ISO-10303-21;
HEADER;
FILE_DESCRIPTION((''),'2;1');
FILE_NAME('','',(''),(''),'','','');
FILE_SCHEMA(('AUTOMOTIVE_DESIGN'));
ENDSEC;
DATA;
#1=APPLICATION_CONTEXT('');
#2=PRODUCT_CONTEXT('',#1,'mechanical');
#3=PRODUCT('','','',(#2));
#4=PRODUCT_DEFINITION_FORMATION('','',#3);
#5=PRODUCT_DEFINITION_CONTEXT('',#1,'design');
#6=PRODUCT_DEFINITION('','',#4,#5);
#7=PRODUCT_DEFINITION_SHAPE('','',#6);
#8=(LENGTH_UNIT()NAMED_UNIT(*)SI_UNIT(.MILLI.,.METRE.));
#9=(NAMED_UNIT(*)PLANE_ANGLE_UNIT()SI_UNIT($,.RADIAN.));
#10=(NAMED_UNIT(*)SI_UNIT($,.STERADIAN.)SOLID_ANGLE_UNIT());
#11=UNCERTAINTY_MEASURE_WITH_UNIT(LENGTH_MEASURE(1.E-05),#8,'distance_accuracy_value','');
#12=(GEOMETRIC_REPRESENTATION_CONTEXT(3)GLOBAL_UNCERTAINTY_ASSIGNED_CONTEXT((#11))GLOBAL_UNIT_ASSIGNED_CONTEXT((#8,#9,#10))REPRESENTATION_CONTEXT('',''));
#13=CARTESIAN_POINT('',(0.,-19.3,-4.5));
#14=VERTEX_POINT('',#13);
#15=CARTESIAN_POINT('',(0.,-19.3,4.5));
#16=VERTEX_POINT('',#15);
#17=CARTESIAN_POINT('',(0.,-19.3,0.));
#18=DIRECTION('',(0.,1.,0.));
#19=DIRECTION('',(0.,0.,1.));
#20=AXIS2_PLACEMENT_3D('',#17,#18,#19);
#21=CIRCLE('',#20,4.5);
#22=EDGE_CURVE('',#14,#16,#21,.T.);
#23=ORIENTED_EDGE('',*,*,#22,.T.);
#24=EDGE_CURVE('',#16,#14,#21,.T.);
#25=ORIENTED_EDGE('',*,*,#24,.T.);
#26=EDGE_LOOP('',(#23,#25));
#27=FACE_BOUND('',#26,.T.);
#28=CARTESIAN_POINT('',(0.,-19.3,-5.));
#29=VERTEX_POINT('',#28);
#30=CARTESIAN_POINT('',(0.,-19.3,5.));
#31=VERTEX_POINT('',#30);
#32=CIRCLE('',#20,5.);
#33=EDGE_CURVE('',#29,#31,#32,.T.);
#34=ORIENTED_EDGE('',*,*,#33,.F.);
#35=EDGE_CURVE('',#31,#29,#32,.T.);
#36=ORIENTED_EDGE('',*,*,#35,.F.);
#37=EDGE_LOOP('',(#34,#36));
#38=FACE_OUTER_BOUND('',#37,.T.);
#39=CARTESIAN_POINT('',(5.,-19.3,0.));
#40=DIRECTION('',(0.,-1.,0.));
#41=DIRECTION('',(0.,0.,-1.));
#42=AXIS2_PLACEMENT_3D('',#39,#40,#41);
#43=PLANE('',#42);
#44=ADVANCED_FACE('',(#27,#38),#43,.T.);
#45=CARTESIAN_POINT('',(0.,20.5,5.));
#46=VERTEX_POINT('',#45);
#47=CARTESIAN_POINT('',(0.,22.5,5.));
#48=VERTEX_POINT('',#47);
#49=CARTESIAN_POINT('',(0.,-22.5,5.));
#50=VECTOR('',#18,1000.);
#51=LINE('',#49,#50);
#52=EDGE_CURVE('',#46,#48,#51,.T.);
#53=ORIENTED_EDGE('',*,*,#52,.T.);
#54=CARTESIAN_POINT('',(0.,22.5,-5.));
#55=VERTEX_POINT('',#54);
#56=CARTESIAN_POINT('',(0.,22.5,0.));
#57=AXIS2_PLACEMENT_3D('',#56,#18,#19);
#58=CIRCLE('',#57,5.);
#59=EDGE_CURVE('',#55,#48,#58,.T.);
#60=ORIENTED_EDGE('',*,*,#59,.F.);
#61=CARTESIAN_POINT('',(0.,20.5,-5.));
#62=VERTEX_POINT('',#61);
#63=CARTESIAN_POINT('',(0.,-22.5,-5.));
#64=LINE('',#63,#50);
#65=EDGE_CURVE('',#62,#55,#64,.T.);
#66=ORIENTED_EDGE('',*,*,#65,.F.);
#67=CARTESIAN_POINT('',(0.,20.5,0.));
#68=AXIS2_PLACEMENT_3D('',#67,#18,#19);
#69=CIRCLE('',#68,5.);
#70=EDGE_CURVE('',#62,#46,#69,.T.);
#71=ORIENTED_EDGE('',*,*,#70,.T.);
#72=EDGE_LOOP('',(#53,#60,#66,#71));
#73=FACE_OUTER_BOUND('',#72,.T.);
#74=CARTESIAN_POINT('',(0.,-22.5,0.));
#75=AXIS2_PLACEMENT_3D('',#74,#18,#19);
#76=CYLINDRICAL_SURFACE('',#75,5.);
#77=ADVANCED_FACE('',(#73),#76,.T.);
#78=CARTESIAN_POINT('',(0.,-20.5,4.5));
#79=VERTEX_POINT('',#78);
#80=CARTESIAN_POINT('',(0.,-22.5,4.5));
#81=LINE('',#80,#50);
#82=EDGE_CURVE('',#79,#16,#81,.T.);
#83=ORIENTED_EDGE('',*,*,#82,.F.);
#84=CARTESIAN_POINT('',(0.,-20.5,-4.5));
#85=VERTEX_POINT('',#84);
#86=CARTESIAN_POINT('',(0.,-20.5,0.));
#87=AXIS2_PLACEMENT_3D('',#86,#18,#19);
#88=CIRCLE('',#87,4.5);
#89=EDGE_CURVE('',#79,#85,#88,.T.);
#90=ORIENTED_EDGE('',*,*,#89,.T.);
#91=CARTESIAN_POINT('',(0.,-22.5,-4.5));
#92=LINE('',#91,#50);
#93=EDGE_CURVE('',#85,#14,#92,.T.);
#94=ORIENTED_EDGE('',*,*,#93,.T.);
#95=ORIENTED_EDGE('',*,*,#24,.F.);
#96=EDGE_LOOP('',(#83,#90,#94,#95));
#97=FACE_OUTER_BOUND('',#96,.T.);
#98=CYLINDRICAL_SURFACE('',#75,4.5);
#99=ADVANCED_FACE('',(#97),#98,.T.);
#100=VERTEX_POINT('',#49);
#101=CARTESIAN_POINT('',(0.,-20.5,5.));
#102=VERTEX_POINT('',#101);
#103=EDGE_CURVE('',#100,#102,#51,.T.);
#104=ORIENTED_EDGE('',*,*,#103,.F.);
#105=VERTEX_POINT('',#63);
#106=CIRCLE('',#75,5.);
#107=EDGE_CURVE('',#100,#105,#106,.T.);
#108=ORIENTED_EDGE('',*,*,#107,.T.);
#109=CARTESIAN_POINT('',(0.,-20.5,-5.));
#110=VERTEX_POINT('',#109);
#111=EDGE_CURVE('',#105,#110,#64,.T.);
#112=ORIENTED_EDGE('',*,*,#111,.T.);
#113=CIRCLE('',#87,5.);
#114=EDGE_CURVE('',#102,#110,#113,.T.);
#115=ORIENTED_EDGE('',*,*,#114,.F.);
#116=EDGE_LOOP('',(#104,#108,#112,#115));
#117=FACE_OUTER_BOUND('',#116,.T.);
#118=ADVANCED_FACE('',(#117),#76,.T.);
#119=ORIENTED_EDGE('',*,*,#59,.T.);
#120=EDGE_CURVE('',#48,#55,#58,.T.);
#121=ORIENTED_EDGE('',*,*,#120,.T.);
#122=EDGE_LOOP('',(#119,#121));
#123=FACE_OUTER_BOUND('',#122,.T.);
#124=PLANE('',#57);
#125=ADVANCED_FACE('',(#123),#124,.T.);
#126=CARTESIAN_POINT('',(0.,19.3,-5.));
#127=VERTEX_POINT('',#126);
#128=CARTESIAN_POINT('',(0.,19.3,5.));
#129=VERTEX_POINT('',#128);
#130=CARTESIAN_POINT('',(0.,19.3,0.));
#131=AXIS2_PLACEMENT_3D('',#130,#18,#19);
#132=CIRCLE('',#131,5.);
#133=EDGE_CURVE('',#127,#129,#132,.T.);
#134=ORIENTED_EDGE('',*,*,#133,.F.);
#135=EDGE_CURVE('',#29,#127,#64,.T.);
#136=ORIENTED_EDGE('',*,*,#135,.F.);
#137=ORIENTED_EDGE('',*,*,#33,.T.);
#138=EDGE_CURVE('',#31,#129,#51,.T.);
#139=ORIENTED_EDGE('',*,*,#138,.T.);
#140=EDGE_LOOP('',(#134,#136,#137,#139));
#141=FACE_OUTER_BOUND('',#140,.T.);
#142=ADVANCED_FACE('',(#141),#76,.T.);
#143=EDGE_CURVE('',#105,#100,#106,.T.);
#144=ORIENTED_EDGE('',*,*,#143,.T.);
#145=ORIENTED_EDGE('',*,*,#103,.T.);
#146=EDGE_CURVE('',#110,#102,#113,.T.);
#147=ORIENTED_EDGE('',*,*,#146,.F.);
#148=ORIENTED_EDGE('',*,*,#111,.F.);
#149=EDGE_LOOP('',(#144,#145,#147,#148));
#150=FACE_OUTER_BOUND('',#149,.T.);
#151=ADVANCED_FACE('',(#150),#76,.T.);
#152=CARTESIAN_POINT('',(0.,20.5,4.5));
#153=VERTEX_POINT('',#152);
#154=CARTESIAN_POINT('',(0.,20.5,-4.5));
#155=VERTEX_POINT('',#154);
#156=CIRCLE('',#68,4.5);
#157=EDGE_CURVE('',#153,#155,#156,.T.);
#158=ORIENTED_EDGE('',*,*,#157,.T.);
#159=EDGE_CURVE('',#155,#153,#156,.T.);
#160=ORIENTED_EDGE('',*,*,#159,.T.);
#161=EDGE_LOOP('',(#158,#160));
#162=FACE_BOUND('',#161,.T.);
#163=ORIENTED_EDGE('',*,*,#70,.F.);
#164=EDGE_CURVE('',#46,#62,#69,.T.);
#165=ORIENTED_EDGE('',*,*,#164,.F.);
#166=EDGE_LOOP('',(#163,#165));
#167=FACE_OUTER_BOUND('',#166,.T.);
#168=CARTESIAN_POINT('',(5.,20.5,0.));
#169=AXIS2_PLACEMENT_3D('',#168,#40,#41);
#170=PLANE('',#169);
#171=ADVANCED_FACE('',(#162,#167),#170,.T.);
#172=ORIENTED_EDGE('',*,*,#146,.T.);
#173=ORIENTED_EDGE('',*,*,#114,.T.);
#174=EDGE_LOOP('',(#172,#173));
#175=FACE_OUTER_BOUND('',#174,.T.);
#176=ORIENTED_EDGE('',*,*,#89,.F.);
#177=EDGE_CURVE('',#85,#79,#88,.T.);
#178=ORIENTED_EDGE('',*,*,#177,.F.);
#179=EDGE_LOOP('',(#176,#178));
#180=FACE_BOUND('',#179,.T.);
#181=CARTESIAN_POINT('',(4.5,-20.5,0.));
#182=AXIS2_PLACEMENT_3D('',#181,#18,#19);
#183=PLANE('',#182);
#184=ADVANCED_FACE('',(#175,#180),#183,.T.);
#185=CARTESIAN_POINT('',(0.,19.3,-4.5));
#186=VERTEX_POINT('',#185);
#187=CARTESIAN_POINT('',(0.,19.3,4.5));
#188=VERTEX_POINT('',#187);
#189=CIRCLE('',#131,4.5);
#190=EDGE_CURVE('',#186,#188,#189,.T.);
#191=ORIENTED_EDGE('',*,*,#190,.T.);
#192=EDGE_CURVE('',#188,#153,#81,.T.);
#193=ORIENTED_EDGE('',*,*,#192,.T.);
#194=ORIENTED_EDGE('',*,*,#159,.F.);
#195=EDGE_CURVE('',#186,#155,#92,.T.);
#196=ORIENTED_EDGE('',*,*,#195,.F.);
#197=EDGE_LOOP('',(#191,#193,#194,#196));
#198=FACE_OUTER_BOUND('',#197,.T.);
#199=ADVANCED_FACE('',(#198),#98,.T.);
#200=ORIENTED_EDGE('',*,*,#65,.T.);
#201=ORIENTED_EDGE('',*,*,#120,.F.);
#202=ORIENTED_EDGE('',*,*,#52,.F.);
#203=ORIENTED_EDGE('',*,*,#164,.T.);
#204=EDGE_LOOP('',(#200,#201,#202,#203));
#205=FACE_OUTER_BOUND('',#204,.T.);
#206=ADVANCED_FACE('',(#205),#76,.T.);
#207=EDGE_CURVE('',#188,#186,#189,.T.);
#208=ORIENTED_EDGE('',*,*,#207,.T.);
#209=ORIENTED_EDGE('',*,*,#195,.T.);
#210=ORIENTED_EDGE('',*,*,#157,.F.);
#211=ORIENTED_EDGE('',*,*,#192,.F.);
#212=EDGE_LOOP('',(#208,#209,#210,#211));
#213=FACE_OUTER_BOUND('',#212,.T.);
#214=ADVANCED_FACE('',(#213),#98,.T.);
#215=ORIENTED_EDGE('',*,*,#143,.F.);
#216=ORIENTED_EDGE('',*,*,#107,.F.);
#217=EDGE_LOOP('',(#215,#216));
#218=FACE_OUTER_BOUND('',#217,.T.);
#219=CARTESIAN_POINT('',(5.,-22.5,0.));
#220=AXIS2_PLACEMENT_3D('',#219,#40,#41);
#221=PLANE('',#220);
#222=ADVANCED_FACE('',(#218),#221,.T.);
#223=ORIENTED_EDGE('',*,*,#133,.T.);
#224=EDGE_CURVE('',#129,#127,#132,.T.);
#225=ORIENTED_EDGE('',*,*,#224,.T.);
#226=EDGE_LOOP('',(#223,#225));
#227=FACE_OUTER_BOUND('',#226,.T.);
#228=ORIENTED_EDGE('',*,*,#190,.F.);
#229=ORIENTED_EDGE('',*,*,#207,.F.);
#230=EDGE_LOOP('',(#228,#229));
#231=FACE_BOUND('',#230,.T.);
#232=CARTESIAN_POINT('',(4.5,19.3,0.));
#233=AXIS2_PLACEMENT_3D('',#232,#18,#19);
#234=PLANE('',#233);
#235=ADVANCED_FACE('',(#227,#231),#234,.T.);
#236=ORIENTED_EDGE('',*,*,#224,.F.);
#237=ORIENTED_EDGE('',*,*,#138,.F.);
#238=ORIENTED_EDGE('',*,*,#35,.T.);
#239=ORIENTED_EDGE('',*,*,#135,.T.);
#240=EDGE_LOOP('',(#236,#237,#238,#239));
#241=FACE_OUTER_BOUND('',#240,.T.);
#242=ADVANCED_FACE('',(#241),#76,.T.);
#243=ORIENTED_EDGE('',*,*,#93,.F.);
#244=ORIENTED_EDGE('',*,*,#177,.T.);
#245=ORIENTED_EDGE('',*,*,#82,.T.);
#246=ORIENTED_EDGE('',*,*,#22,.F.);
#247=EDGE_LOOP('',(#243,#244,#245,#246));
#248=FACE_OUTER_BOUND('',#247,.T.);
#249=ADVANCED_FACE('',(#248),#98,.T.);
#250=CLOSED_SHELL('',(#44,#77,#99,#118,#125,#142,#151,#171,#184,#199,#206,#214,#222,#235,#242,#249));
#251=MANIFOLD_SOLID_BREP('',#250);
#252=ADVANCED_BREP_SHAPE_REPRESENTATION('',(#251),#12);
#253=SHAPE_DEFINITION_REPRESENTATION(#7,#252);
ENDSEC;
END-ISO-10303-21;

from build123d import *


with BuildPart() as part:
    # 草图1 → 旋转1 (revolve)
    with BuildSketch(Plane(origin=(0, 0, 0), x_dir=(-1, 0, 0), z_dir=(0, 0, -1)), mode=Mode.PRIVATE) as revolve_1_sk:
        Polygon((-5, -22.5), (0, -22.5), (0, 22.5), (-5, 22.5), (-5, 20.5), (-4.5, 20.5), (-4.5, 19.3), (-5, 19.3), (-5, -19.3), (-4.5, -19.3), (-4.5, -20.5), (-5, -20.5), align=None)
    revolve(revolve_1_sk.sketch.rotate(Axis((0, -22.5, 0), (0, 1, 0)), 270), axis=Axis((0, -22.5, 0), (0, 1, 0)))


solid = part.part
